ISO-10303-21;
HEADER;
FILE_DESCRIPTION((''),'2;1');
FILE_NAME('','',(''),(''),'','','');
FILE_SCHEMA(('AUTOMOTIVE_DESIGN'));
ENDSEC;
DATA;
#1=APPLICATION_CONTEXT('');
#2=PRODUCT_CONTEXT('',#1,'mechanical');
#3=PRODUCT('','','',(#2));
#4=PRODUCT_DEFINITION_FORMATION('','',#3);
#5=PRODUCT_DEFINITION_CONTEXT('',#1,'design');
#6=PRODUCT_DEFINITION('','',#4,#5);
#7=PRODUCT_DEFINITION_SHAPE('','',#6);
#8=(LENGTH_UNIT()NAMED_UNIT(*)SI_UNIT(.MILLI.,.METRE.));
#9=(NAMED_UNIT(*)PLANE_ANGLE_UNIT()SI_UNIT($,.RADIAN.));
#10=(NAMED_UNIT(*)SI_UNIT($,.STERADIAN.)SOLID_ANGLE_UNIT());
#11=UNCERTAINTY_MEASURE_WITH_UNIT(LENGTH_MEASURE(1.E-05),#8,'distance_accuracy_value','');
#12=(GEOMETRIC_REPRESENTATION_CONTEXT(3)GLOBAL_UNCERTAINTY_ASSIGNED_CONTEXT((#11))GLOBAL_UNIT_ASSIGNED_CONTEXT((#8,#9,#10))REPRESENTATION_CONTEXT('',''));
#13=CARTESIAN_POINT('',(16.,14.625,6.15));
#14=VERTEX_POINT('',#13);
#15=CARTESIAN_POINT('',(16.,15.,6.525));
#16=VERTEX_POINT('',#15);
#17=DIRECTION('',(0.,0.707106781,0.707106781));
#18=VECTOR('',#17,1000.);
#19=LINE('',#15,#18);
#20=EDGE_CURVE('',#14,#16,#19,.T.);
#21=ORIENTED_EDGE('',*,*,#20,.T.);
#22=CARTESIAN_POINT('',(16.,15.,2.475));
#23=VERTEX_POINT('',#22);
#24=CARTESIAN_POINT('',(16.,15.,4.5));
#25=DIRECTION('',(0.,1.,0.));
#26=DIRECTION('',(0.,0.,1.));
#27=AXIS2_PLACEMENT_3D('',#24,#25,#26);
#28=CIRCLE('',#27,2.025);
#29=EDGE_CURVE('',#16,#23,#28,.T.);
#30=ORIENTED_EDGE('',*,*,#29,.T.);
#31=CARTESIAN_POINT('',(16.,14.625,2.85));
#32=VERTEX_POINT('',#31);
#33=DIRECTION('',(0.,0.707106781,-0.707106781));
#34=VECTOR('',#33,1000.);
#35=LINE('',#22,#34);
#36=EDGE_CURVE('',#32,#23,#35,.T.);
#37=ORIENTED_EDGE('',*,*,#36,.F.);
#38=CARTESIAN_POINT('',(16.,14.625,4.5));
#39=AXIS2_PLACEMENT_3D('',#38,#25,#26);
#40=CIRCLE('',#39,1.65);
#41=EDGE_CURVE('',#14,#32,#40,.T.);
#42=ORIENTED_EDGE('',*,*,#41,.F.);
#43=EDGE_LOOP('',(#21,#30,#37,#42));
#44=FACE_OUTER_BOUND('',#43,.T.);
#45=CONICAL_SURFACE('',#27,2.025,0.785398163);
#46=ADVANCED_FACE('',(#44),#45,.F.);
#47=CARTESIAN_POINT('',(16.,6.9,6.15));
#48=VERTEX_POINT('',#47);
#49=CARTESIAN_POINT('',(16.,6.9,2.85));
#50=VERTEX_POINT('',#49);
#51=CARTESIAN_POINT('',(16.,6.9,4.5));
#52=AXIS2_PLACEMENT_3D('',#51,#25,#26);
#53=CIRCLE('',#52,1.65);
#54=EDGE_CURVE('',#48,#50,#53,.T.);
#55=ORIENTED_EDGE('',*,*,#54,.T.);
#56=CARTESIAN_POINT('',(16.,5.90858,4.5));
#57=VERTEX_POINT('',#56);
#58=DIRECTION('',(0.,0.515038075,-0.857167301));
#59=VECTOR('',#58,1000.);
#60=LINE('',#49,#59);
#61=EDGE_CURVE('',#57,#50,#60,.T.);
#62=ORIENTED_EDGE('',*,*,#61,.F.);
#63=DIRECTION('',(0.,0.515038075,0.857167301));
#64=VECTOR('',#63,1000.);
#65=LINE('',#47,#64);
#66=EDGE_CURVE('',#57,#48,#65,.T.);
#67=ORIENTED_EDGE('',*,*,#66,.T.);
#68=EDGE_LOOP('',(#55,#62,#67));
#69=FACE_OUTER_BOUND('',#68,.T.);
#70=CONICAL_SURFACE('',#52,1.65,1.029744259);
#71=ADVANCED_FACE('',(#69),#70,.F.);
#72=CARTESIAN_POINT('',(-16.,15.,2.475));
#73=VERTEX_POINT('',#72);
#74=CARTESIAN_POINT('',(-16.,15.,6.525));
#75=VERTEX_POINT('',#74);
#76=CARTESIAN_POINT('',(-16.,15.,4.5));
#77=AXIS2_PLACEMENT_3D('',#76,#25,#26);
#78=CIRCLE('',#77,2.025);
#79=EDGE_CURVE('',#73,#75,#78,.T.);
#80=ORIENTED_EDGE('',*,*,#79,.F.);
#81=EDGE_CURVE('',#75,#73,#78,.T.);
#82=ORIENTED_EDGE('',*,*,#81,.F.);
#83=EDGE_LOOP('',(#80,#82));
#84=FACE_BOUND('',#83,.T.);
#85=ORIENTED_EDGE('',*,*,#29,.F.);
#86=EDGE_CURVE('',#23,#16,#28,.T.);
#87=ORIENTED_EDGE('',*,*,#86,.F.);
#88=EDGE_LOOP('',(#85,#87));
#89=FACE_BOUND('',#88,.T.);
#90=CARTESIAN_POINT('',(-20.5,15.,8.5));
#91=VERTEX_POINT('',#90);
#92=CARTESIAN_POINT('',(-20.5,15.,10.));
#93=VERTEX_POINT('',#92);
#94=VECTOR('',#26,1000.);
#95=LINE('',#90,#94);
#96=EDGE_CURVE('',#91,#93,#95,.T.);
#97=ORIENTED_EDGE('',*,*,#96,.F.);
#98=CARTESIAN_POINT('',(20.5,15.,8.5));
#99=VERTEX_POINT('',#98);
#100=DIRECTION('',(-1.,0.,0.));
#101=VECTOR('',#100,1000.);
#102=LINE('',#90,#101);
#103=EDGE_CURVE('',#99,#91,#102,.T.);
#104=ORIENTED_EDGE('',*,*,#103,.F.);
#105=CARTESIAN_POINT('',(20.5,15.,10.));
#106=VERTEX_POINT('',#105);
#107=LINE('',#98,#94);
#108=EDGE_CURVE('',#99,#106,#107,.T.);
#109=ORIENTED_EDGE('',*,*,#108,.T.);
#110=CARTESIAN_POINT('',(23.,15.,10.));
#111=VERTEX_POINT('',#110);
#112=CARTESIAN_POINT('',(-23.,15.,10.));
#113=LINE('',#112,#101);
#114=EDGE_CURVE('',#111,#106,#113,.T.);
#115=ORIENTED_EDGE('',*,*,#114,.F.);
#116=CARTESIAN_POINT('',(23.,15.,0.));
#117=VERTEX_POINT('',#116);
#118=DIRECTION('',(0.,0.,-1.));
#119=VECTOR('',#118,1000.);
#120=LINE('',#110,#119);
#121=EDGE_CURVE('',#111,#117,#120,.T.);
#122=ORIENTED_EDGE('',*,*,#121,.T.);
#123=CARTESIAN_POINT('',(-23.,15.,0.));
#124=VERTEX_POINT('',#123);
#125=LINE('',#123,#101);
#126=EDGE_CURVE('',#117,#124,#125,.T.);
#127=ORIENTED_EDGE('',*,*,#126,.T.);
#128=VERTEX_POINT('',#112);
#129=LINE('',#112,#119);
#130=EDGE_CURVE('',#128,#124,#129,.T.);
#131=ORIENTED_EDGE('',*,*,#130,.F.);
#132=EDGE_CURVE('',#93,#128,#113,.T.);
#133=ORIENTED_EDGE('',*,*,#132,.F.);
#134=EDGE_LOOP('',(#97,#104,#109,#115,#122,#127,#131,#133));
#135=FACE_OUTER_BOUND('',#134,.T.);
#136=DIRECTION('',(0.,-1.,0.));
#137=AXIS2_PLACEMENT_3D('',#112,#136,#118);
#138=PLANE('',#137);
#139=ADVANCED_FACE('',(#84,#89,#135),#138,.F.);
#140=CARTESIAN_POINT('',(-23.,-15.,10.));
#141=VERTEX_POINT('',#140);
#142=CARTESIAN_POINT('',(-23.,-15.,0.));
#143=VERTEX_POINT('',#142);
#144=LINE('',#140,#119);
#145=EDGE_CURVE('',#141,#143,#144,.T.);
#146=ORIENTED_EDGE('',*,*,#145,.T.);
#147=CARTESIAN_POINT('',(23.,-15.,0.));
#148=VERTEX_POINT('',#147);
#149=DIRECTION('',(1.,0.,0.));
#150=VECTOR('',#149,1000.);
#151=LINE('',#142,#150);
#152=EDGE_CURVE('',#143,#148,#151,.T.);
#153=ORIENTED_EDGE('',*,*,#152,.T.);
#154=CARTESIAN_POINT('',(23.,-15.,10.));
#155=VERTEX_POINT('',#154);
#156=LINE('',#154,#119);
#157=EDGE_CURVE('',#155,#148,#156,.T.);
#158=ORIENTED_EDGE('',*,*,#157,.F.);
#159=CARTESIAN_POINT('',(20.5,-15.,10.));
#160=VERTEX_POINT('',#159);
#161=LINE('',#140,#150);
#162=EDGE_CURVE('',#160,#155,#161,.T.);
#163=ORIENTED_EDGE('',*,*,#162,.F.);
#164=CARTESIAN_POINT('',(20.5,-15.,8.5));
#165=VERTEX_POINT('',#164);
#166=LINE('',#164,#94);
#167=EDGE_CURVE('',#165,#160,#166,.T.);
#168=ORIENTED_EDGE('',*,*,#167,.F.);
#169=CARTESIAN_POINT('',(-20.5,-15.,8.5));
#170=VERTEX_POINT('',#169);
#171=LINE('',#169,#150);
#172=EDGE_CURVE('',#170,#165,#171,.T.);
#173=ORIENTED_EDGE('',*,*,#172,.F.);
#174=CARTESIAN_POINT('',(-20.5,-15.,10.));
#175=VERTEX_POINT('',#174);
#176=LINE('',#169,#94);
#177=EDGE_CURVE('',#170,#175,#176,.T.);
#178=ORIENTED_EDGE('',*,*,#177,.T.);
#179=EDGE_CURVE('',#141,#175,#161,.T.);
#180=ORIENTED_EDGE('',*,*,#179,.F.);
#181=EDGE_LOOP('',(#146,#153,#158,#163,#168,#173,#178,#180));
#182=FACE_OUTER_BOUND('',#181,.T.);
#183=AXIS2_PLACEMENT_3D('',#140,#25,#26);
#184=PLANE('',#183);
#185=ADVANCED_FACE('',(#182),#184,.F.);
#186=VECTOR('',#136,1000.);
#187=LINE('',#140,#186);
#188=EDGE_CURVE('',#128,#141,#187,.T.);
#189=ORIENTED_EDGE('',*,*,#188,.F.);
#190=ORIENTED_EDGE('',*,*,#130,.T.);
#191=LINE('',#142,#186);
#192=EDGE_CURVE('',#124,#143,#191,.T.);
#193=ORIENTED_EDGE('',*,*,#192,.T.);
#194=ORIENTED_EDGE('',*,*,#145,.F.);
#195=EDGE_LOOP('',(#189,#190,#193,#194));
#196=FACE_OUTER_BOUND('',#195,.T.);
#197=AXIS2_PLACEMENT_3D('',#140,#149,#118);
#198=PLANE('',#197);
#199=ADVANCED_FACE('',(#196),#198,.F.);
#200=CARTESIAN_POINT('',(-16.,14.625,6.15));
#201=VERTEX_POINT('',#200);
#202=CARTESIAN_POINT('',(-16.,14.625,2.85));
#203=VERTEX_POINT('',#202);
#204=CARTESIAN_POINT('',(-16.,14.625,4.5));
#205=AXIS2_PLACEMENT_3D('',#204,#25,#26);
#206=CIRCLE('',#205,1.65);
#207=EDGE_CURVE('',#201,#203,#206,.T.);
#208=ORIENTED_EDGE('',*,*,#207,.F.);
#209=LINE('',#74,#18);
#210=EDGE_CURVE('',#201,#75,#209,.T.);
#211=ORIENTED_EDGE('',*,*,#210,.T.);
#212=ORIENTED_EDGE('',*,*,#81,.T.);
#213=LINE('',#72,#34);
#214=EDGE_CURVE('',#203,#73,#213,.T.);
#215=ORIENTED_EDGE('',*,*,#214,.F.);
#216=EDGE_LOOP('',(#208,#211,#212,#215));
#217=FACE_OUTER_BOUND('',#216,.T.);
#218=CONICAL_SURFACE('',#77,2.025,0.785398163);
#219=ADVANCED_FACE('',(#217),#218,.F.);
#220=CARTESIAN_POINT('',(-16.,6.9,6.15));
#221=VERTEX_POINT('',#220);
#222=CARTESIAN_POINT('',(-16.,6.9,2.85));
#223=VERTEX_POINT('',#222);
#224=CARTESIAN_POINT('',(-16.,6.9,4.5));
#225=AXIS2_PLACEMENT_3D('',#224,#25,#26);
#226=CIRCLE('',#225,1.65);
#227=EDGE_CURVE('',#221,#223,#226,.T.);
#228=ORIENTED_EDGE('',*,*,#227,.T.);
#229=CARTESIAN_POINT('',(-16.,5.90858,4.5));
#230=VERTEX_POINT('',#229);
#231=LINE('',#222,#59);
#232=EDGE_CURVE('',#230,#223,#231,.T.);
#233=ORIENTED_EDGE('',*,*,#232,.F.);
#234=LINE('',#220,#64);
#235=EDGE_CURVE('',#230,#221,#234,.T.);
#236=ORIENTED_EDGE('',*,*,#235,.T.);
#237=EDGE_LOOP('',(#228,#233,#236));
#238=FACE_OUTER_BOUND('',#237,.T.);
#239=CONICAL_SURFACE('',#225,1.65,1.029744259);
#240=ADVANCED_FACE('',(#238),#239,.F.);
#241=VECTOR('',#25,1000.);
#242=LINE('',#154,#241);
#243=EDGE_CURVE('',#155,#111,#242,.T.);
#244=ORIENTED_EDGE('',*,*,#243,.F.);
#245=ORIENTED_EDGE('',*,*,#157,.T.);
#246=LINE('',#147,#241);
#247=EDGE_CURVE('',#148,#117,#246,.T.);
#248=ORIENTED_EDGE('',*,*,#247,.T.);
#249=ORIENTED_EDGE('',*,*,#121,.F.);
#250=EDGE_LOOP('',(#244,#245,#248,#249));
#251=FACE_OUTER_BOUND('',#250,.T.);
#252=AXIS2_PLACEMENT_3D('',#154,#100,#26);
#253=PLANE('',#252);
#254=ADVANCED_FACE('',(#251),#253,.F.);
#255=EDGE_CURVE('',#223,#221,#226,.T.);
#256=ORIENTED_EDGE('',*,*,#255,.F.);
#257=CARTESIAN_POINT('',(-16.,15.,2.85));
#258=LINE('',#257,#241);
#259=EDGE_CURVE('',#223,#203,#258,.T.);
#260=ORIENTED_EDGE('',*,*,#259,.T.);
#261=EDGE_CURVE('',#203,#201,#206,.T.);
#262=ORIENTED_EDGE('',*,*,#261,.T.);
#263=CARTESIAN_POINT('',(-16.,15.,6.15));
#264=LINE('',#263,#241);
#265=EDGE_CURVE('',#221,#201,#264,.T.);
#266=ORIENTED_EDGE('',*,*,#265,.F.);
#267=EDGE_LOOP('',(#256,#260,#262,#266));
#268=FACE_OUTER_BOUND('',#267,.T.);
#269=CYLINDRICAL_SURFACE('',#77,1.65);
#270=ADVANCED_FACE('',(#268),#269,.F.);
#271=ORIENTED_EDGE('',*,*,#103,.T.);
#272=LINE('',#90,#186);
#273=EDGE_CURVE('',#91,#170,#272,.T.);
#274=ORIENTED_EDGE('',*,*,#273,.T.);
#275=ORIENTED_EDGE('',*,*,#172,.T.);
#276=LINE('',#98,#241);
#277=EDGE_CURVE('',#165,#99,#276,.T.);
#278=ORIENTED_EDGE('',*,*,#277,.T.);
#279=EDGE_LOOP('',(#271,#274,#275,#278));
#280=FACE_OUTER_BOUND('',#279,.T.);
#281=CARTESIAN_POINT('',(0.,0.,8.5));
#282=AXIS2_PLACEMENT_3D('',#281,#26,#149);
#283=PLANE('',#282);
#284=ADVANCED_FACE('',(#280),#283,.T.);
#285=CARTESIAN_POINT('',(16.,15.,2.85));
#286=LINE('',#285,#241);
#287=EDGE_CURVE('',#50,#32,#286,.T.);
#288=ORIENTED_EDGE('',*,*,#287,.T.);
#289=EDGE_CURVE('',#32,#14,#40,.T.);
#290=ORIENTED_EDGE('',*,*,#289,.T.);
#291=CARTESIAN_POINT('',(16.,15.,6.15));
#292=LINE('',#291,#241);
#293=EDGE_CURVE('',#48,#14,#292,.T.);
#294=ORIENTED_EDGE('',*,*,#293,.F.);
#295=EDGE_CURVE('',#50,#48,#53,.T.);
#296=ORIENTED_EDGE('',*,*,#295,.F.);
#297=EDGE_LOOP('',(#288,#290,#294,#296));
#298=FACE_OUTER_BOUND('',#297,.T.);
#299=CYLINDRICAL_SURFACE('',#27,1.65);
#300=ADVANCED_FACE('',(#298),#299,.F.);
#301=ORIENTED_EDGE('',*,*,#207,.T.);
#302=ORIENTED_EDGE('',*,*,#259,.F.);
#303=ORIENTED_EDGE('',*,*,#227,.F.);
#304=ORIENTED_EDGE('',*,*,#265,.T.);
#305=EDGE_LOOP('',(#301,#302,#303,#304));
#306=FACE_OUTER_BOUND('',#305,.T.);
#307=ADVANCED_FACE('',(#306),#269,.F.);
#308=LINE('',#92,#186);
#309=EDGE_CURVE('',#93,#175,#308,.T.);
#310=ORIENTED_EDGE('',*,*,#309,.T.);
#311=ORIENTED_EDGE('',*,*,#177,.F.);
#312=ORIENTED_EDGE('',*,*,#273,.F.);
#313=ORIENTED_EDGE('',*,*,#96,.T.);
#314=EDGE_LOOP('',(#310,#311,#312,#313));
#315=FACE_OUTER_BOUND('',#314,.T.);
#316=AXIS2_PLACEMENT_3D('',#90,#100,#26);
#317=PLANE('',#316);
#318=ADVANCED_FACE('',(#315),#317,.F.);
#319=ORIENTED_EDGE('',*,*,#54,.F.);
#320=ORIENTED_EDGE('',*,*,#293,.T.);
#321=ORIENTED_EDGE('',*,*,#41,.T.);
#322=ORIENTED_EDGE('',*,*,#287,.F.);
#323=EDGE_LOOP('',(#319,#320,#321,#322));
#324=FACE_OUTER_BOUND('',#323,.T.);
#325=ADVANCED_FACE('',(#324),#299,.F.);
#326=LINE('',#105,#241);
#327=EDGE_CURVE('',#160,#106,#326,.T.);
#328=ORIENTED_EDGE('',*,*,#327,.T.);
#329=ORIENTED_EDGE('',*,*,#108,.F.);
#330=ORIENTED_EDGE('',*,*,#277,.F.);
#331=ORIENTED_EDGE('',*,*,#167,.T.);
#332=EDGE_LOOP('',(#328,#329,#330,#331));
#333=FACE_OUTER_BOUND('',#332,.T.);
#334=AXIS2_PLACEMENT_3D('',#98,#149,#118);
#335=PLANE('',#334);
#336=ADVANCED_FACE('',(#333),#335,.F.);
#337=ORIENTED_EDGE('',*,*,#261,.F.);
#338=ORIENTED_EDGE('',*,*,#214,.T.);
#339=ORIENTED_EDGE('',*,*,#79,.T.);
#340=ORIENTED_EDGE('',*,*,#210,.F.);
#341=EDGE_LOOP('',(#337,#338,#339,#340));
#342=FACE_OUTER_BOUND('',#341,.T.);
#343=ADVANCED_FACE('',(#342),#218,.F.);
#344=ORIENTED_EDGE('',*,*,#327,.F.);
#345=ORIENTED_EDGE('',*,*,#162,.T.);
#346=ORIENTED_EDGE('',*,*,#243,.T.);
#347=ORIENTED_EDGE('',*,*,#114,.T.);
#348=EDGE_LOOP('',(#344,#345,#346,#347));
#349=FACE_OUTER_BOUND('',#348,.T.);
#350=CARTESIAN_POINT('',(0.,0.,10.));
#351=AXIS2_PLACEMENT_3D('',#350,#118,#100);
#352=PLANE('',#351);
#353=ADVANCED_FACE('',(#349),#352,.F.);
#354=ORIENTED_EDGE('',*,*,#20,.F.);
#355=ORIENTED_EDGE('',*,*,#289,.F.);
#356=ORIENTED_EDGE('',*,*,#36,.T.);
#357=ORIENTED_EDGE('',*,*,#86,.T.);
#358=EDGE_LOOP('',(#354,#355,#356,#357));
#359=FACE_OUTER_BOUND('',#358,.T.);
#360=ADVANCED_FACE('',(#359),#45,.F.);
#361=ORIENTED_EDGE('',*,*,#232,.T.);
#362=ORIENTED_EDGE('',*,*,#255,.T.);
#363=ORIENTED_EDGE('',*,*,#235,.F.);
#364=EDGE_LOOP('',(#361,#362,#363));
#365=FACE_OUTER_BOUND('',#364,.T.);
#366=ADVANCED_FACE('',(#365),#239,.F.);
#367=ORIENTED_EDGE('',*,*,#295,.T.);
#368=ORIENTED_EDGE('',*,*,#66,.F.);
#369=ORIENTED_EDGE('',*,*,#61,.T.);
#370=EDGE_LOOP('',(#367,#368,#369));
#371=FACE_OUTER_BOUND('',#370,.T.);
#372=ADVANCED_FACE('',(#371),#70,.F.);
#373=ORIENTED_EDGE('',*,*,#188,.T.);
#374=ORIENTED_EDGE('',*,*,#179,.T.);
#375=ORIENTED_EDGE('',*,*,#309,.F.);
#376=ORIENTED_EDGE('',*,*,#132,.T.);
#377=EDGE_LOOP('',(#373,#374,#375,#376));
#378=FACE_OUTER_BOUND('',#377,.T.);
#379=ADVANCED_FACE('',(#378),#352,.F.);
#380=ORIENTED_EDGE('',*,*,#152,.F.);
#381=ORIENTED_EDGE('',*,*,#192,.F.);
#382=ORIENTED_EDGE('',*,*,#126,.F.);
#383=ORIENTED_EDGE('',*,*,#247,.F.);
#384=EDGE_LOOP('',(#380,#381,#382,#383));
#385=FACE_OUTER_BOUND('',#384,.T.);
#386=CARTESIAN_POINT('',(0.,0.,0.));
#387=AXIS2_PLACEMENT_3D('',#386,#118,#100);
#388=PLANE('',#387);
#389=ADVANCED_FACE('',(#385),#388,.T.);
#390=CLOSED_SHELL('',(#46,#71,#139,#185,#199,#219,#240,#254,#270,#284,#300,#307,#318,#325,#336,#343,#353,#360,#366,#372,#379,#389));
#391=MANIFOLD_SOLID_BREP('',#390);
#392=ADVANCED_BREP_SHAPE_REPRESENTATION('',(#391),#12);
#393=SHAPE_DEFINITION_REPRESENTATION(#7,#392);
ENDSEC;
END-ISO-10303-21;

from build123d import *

# Parameters (mm, degrees)
SKETCH_1_W          = 46
SKETCH_1_H          = 30
EXTRUDE_1_DEPTH     = 10
SKETCH_2_W          = 41
SKETCH_2_H          = 30
CUT_EXTRUDE_1_DEPTH = 1.5


with BuildPart() as part:
    # 草图1 → 凸台-拉伸1 (new body)
    with BuildSketch(Plane.XY):
        Rectangle(SKETCH_1_W, SKETCH_1_H)
    extrude(amount=EXTRUDE_1_DEPTH)

    # 草图2 → 切除-拉伸1 (cut)
    with BuildSketch(Plane.XY.offset(10)):
        Rectangle(SKETCH_2_W, SKETCH_2_H)
    extrude(amount=-CUT_EXTRUDE_1_DEPTH, mode=Mode.SUBTRACT)

    # 草图3 → M4 螺纹孔1 (revolve, cut)
    with BuildSketch(Plane(origin=(16, 15, 4.5), x_dir=(0, 0, 1), z_dir=(1, 0, 0))):
        Polygon((0, 0), (0, 9.091420021), (1.65, 8.1), (1.65, 0.375), (2.025, 0), align=None)
    hole_wizard_m4_1 = revolve(axis=Axis((16, 21.35, 4.5), (0, -1, 0)), mode=Mode.SUBTRACT)

    # 镜向1: M4 螺纹孔1 across plane
    add(hole_wizard_m4_1.mirror(Plane(origin=(0, 0, 0), x_dir=(0, 0, 1), z_dir=(1, 0, 0))), mode=Mode.SUBTRACT)


solid = part.part
